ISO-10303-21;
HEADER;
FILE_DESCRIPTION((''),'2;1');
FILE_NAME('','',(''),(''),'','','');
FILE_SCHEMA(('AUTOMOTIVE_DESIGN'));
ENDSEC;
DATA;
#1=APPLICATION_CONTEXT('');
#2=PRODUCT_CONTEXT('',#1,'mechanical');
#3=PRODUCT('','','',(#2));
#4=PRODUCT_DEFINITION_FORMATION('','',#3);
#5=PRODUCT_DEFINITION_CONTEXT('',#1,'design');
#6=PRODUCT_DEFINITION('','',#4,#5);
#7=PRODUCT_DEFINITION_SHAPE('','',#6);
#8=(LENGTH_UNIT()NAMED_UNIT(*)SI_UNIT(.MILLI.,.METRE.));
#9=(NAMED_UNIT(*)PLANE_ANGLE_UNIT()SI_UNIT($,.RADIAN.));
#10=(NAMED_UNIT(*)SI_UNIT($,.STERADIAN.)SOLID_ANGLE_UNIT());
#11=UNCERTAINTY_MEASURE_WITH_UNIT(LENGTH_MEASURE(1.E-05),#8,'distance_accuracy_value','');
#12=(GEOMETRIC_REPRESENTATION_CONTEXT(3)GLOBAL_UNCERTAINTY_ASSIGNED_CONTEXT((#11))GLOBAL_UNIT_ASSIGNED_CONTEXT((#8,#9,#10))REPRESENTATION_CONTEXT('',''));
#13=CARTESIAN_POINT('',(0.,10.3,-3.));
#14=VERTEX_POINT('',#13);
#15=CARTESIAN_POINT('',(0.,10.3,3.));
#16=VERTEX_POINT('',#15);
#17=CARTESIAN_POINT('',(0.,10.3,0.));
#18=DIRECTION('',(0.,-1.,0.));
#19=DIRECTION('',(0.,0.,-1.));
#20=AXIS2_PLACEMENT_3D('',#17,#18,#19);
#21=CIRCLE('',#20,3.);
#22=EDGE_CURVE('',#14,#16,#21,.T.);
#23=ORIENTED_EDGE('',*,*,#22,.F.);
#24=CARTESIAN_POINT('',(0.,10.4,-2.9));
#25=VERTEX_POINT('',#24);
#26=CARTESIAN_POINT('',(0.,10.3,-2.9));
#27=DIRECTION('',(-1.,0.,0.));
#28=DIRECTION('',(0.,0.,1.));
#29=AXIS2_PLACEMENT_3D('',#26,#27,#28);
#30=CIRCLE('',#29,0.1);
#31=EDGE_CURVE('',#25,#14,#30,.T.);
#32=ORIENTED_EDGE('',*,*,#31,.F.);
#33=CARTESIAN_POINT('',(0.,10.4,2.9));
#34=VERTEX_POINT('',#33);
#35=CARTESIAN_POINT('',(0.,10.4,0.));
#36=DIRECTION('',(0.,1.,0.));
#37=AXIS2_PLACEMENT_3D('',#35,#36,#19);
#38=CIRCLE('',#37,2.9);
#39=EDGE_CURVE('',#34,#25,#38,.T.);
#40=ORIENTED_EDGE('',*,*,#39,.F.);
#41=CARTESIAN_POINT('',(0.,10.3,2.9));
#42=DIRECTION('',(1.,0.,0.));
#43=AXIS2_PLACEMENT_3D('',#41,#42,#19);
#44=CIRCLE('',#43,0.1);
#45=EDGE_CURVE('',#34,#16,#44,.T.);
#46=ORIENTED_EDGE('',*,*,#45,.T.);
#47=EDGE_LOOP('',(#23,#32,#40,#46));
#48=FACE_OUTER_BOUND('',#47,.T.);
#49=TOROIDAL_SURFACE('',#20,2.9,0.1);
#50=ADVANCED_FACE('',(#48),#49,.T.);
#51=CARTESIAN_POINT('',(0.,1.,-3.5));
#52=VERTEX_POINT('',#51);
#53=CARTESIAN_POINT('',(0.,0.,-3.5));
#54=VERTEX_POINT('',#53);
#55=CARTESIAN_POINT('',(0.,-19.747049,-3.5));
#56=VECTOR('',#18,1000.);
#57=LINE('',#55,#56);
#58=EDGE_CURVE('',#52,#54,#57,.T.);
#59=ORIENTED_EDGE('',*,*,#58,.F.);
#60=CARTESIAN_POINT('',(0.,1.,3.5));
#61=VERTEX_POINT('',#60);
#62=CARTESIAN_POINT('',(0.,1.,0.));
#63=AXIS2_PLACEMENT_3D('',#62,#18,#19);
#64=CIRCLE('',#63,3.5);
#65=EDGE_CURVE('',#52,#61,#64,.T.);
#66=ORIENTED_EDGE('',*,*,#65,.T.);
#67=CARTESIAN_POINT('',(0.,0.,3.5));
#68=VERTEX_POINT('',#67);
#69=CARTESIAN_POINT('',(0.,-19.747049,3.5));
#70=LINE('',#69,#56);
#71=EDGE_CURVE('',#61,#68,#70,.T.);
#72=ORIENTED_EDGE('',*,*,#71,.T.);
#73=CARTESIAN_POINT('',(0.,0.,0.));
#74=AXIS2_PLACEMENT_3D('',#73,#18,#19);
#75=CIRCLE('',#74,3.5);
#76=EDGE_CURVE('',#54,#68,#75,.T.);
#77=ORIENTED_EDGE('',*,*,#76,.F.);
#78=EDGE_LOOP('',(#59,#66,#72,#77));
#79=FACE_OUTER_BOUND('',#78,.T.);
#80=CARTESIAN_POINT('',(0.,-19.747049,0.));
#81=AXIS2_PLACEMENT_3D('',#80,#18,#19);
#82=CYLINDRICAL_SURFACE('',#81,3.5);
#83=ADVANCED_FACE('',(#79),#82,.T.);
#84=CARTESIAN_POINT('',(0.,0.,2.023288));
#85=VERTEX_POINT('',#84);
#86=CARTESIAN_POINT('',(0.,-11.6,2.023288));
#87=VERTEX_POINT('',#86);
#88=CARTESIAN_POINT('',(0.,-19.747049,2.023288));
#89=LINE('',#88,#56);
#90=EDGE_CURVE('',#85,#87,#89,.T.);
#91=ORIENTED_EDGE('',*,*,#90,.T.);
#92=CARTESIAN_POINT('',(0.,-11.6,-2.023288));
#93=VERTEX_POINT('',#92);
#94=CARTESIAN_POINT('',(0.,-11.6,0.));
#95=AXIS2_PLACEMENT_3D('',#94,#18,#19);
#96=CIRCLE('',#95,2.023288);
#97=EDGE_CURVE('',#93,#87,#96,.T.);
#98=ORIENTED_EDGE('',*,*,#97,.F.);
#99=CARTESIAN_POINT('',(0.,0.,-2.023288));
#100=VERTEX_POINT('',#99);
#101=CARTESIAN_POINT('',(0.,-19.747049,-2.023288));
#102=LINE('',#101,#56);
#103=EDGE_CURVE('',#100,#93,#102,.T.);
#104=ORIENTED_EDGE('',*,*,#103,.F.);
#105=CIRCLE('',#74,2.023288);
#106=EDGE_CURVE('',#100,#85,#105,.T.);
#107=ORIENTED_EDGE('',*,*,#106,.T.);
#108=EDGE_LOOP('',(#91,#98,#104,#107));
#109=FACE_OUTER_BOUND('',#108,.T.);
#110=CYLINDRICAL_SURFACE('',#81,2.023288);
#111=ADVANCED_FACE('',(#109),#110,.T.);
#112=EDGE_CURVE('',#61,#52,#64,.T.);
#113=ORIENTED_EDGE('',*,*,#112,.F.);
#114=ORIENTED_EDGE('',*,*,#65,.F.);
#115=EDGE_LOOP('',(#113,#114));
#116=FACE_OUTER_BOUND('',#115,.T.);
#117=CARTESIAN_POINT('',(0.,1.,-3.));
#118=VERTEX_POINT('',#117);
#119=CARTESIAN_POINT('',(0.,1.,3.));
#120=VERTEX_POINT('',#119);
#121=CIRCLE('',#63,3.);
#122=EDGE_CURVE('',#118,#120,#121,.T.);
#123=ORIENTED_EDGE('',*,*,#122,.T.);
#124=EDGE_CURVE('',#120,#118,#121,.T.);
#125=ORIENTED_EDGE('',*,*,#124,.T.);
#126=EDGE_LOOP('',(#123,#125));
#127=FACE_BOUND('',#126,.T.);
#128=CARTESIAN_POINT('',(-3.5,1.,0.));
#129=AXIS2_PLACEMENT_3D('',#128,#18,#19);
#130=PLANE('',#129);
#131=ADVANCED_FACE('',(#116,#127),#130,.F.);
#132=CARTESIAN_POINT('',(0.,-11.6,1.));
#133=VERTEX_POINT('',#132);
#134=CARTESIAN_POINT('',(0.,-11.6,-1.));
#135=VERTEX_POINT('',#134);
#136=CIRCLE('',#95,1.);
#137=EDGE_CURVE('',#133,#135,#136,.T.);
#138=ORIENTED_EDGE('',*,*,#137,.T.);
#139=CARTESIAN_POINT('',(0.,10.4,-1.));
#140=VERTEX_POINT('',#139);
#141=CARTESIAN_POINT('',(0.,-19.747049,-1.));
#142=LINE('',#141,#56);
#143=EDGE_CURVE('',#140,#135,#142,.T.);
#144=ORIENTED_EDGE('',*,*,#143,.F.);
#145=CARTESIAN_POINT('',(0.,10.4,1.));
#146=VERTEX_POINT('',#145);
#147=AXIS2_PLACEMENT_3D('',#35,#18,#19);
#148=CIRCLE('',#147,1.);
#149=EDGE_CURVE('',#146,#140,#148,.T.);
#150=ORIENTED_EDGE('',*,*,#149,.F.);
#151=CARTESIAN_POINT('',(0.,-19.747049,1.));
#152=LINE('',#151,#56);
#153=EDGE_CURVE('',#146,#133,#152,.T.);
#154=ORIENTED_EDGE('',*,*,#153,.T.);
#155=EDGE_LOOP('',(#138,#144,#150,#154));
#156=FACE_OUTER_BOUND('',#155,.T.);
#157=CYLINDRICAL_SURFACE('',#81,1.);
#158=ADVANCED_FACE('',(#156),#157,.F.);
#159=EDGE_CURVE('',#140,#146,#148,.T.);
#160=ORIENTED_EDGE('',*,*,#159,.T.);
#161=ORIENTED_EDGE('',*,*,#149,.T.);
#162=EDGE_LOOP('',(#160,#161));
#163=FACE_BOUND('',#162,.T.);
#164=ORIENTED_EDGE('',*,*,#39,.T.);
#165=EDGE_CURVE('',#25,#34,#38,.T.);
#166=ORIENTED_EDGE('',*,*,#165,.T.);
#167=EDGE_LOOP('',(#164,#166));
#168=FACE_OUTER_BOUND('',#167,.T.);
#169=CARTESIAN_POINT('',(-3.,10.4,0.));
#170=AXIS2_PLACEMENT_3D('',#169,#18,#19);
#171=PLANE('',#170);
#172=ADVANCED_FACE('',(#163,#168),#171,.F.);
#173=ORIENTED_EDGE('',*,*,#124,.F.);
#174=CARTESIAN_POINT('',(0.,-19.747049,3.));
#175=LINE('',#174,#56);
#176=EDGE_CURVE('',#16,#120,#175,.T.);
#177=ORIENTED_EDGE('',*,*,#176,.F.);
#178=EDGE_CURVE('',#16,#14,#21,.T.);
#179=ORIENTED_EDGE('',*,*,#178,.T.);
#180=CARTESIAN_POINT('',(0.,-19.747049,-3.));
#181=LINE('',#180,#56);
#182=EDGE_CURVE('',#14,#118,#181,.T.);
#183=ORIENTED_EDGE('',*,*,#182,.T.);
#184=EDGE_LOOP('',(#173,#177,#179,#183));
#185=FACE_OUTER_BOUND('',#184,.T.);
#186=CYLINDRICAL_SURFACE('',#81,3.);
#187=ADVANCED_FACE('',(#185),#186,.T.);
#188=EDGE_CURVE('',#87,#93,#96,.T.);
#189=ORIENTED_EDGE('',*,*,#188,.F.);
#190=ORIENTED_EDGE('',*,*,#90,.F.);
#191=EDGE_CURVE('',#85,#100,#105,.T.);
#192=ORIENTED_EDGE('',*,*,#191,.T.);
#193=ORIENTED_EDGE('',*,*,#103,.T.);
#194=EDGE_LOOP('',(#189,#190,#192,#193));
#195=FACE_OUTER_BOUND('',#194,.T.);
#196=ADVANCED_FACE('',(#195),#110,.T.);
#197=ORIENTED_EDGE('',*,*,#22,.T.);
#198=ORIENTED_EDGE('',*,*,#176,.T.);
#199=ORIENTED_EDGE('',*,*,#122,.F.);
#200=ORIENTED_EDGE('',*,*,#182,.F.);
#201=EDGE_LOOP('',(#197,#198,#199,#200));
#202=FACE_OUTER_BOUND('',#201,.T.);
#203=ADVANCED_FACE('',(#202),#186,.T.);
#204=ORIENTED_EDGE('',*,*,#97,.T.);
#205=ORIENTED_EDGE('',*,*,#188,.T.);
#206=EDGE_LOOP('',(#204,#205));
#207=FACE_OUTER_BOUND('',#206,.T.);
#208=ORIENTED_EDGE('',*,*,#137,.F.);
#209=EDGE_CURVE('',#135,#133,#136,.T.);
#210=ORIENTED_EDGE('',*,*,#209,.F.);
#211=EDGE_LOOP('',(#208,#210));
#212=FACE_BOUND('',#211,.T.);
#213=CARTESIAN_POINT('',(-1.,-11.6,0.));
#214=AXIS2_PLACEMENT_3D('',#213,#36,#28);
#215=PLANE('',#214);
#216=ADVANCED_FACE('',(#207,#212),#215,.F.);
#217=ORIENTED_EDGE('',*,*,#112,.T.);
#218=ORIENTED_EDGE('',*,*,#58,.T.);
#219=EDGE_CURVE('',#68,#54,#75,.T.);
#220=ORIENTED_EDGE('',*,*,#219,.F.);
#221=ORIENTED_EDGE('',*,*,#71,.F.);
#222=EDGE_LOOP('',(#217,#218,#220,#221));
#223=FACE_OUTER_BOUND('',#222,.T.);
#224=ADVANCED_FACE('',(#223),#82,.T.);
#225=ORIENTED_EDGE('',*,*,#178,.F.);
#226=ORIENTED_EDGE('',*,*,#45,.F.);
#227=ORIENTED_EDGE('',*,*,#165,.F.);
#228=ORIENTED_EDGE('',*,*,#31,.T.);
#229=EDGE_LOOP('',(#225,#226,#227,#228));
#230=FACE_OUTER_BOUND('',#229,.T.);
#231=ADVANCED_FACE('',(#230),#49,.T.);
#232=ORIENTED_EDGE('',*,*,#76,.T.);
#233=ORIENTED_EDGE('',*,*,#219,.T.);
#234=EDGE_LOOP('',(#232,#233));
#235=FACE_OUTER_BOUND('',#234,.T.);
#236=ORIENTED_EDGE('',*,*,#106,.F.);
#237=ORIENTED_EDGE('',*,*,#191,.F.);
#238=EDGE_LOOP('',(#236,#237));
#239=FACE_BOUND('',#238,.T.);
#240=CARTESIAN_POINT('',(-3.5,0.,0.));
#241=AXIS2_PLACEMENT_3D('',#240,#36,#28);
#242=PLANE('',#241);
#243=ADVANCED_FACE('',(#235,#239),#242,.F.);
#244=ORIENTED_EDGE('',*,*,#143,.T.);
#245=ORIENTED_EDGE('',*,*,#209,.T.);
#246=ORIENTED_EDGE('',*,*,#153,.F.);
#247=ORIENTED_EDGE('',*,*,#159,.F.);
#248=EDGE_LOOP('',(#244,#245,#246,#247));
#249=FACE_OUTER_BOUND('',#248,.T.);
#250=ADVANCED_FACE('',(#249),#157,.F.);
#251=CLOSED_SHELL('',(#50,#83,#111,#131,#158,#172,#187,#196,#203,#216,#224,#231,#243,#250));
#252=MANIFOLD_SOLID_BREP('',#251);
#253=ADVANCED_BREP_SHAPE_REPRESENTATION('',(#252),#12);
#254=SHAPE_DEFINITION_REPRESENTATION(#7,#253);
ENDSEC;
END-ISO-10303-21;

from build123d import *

# Parameters (mm, degrees)
FILLET3_R = 0.1


with BuildPart() as part:
    # Sketch1 → Revolve1 (revolve)
    with BuildSketch(Plane.XY, mode=Mode.PRIVATE) as revolve1_sk:
        Polygon((-3.5, 0), (-2.02328752, 0), (-2.02328752, -11.6), (-1, -11.6), (-1, 10.4), (-3, 10.4), (-3, 1), (-3.5, 1), align=None)
    revolve(revolve1_sk.sketch.rotate(Axis((0, -19.747048695, 0), (0, 1, 0)), 270), axis=Axis((0, -19.747048695, 0), (0, 1, 0)))

    # Fillet3
    fillet3_edges = [part.edges().sort_by_distance(p)[0] for p in [
        (0, 10.4, 3),
    ]]
    fillet(fillet3_edges, radius=FILLET3_R)


solid = part.part
